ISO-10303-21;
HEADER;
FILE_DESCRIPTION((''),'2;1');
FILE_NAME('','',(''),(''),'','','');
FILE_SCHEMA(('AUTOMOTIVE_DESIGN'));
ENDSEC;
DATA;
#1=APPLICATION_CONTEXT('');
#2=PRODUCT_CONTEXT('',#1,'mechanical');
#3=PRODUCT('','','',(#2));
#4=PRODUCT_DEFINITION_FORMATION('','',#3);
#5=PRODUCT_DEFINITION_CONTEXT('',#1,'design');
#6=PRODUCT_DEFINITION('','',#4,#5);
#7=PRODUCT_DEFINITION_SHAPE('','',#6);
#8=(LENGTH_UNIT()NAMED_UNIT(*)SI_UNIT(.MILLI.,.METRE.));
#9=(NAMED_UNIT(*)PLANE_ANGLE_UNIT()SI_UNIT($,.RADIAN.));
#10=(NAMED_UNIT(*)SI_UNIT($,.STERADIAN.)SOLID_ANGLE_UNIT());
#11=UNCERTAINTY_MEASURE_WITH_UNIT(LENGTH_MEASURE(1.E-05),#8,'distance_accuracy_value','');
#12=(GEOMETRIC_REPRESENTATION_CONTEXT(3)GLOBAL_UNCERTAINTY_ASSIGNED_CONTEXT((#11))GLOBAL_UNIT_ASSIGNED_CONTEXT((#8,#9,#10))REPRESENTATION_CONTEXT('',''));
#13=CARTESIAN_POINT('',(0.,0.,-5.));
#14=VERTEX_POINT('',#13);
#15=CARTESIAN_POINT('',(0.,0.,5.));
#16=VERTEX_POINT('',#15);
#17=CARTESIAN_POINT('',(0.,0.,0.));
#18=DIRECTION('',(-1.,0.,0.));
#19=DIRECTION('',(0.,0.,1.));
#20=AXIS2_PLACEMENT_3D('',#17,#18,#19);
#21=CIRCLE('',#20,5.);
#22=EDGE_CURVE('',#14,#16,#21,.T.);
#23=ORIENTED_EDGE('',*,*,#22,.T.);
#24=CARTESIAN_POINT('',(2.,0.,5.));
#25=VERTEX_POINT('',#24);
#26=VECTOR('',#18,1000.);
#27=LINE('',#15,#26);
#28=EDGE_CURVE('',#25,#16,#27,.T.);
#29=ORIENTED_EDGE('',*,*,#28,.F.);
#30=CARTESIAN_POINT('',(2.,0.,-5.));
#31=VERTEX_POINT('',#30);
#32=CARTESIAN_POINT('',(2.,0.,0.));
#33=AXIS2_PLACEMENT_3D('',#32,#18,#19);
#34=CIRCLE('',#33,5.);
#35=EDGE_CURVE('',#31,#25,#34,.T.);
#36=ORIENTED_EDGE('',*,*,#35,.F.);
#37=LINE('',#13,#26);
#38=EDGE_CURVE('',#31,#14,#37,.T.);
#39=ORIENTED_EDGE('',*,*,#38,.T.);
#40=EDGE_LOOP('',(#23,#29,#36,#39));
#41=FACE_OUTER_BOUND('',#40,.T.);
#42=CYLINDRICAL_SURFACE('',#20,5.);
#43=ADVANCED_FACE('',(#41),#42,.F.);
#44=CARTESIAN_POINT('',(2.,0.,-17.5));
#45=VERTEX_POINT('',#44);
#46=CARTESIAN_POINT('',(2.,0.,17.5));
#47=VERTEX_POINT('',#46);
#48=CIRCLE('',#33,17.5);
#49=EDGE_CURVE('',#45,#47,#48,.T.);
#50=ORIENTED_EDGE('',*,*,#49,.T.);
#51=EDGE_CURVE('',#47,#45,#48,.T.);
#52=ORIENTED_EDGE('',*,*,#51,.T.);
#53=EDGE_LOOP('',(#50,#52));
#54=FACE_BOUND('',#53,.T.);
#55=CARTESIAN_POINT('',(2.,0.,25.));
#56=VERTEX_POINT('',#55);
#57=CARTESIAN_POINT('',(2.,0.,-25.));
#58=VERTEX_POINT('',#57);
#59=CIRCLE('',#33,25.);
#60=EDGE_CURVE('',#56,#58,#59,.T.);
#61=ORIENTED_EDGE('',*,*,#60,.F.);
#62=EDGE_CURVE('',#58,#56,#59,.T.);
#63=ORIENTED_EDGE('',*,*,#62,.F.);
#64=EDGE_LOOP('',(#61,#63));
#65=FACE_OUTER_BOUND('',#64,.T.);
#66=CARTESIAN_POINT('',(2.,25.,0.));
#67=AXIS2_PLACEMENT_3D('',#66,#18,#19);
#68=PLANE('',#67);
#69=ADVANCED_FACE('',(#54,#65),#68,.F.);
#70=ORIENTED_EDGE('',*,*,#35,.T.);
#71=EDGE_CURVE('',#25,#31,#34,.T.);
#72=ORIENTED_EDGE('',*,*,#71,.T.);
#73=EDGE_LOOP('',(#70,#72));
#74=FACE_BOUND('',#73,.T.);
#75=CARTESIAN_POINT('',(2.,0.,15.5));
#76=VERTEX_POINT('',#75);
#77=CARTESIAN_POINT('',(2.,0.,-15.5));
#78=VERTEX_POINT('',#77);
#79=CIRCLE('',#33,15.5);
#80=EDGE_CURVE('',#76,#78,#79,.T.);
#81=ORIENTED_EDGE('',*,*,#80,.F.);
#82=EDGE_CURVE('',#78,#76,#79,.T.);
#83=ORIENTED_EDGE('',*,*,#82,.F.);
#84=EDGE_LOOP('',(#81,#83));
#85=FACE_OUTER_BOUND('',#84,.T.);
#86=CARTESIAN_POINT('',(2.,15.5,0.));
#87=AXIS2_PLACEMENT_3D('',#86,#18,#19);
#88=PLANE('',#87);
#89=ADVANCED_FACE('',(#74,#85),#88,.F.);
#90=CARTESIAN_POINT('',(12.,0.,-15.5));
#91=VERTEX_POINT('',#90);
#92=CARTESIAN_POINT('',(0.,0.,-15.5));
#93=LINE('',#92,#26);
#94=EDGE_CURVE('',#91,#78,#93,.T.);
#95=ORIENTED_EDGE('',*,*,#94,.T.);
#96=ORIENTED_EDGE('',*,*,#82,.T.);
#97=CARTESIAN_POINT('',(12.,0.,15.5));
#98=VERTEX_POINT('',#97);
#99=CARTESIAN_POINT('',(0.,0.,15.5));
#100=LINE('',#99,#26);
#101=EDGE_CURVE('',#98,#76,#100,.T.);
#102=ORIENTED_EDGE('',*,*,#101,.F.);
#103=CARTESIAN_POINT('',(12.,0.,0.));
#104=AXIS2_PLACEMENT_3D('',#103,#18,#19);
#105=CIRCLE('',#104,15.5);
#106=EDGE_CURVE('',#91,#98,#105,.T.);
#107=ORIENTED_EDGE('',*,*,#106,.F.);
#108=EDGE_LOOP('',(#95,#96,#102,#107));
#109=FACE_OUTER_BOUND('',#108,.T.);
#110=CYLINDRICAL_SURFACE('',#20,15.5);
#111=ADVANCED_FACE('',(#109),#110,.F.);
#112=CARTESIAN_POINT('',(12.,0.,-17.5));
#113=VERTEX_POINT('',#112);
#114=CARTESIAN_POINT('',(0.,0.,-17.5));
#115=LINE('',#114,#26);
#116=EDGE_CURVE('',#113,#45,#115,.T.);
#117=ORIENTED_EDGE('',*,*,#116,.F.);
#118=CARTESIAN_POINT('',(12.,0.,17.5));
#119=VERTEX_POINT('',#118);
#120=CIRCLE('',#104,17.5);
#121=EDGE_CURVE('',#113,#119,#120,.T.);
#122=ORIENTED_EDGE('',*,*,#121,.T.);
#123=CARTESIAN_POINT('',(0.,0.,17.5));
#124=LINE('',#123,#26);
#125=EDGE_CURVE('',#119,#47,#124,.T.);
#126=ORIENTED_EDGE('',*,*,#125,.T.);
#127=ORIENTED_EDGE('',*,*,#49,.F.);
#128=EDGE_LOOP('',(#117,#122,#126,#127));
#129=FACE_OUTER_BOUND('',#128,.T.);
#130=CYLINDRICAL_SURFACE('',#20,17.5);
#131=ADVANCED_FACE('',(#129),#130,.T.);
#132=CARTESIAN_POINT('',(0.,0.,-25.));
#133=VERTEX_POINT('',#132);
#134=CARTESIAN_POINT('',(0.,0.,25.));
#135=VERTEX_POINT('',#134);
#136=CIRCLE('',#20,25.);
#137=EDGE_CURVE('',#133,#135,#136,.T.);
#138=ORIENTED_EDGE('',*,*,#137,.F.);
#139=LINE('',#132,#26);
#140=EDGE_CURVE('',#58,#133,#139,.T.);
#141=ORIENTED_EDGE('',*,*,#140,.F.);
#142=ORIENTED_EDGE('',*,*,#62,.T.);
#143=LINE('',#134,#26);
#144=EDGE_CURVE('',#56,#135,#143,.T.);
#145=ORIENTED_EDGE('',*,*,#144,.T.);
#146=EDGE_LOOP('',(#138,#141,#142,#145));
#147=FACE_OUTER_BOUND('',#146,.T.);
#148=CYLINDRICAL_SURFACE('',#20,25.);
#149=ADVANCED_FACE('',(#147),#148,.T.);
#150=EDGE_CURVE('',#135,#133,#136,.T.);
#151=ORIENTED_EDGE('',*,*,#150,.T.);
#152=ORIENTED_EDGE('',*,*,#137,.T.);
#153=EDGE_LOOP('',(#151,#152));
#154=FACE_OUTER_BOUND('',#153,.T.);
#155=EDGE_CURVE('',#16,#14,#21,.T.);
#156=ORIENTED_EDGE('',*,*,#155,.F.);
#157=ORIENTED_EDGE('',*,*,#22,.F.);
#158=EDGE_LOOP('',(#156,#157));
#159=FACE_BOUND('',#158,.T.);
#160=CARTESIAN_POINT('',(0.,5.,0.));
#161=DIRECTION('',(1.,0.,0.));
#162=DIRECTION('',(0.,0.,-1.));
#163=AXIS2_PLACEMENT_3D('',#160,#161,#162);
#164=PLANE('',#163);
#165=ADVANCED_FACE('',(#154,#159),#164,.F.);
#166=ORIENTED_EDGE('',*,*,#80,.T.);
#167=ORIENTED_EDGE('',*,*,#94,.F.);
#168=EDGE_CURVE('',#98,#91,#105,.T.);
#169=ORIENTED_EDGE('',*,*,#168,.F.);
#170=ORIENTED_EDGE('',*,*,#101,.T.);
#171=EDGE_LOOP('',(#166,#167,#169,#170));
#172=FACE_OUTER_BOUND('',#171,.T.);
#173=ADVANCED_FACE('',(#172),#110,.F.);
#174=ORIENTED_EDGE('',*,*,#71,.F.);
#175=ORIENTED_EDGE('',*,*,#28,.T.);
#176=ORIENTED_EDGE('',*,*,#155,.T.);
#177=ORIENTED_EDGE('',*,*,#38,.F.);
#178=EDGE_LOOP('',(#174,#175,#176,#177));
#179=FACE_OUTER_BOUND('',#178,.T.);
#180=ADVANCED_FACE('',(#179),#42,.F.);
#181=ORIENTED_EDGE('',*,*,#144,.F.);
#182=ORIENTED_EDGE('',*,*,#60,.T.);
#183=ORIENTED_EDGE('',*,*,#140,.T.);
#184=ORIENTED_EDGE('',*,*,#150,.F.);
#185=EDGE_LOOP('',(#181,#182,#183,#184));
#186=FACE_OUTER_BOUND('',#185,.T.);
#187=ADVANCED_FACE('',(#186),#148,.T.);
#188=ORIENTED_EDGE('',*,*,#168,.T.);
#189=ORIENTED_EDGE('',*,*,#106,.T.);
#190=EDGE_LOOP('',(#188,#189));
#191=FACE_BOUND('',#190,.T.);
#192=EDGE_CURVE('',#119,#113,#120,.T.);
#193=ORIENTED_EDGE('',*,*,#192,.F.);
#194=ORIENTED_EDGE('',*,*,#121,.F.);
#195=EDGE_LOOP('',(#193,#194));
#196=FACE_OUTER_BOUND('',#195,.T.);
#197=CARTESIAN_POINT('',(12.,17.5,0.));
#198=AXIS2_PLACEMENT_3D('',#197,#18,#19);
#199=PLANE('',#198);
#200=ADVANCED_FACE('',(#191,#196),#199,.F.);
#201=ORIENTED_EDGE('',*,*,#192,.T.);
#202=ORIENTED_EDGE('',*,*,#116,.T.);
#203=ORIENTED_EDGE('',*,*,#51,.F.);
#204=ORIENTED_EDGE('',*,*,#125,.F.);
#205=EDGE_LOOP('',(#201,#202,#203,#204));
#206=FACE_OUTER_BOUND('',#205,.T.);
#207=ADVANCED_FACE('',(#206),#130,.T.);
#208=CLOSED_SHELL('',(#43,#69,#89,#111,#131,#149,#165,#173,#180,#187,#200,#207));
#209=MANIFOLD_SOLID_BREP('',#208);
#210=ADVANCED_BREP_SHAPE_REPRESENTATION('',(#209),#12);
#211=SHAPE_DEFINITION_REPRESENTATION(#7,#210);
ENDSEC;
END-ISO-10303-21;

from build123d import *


with BuildPart() as part:
    # 草图1 → 旋转1 (revolve)
    with BuildSketch(Plane.XY, mode=Mode.PRIVATE) as revolve_1_sk:
        Polygon((0, 25), (2, 25), (2, 17.5), (12, 17.5), (12, 15.5), (2, 15.5), (2, 5), (0, 5), align=None)
    revolve(revolve_1_sk.sketch.rotate(Axis((0, 0, 0), (1, 0, 0)), 90), axis=Axis((0, 0, 0), (1, 0, 0)))


solid = part.part
